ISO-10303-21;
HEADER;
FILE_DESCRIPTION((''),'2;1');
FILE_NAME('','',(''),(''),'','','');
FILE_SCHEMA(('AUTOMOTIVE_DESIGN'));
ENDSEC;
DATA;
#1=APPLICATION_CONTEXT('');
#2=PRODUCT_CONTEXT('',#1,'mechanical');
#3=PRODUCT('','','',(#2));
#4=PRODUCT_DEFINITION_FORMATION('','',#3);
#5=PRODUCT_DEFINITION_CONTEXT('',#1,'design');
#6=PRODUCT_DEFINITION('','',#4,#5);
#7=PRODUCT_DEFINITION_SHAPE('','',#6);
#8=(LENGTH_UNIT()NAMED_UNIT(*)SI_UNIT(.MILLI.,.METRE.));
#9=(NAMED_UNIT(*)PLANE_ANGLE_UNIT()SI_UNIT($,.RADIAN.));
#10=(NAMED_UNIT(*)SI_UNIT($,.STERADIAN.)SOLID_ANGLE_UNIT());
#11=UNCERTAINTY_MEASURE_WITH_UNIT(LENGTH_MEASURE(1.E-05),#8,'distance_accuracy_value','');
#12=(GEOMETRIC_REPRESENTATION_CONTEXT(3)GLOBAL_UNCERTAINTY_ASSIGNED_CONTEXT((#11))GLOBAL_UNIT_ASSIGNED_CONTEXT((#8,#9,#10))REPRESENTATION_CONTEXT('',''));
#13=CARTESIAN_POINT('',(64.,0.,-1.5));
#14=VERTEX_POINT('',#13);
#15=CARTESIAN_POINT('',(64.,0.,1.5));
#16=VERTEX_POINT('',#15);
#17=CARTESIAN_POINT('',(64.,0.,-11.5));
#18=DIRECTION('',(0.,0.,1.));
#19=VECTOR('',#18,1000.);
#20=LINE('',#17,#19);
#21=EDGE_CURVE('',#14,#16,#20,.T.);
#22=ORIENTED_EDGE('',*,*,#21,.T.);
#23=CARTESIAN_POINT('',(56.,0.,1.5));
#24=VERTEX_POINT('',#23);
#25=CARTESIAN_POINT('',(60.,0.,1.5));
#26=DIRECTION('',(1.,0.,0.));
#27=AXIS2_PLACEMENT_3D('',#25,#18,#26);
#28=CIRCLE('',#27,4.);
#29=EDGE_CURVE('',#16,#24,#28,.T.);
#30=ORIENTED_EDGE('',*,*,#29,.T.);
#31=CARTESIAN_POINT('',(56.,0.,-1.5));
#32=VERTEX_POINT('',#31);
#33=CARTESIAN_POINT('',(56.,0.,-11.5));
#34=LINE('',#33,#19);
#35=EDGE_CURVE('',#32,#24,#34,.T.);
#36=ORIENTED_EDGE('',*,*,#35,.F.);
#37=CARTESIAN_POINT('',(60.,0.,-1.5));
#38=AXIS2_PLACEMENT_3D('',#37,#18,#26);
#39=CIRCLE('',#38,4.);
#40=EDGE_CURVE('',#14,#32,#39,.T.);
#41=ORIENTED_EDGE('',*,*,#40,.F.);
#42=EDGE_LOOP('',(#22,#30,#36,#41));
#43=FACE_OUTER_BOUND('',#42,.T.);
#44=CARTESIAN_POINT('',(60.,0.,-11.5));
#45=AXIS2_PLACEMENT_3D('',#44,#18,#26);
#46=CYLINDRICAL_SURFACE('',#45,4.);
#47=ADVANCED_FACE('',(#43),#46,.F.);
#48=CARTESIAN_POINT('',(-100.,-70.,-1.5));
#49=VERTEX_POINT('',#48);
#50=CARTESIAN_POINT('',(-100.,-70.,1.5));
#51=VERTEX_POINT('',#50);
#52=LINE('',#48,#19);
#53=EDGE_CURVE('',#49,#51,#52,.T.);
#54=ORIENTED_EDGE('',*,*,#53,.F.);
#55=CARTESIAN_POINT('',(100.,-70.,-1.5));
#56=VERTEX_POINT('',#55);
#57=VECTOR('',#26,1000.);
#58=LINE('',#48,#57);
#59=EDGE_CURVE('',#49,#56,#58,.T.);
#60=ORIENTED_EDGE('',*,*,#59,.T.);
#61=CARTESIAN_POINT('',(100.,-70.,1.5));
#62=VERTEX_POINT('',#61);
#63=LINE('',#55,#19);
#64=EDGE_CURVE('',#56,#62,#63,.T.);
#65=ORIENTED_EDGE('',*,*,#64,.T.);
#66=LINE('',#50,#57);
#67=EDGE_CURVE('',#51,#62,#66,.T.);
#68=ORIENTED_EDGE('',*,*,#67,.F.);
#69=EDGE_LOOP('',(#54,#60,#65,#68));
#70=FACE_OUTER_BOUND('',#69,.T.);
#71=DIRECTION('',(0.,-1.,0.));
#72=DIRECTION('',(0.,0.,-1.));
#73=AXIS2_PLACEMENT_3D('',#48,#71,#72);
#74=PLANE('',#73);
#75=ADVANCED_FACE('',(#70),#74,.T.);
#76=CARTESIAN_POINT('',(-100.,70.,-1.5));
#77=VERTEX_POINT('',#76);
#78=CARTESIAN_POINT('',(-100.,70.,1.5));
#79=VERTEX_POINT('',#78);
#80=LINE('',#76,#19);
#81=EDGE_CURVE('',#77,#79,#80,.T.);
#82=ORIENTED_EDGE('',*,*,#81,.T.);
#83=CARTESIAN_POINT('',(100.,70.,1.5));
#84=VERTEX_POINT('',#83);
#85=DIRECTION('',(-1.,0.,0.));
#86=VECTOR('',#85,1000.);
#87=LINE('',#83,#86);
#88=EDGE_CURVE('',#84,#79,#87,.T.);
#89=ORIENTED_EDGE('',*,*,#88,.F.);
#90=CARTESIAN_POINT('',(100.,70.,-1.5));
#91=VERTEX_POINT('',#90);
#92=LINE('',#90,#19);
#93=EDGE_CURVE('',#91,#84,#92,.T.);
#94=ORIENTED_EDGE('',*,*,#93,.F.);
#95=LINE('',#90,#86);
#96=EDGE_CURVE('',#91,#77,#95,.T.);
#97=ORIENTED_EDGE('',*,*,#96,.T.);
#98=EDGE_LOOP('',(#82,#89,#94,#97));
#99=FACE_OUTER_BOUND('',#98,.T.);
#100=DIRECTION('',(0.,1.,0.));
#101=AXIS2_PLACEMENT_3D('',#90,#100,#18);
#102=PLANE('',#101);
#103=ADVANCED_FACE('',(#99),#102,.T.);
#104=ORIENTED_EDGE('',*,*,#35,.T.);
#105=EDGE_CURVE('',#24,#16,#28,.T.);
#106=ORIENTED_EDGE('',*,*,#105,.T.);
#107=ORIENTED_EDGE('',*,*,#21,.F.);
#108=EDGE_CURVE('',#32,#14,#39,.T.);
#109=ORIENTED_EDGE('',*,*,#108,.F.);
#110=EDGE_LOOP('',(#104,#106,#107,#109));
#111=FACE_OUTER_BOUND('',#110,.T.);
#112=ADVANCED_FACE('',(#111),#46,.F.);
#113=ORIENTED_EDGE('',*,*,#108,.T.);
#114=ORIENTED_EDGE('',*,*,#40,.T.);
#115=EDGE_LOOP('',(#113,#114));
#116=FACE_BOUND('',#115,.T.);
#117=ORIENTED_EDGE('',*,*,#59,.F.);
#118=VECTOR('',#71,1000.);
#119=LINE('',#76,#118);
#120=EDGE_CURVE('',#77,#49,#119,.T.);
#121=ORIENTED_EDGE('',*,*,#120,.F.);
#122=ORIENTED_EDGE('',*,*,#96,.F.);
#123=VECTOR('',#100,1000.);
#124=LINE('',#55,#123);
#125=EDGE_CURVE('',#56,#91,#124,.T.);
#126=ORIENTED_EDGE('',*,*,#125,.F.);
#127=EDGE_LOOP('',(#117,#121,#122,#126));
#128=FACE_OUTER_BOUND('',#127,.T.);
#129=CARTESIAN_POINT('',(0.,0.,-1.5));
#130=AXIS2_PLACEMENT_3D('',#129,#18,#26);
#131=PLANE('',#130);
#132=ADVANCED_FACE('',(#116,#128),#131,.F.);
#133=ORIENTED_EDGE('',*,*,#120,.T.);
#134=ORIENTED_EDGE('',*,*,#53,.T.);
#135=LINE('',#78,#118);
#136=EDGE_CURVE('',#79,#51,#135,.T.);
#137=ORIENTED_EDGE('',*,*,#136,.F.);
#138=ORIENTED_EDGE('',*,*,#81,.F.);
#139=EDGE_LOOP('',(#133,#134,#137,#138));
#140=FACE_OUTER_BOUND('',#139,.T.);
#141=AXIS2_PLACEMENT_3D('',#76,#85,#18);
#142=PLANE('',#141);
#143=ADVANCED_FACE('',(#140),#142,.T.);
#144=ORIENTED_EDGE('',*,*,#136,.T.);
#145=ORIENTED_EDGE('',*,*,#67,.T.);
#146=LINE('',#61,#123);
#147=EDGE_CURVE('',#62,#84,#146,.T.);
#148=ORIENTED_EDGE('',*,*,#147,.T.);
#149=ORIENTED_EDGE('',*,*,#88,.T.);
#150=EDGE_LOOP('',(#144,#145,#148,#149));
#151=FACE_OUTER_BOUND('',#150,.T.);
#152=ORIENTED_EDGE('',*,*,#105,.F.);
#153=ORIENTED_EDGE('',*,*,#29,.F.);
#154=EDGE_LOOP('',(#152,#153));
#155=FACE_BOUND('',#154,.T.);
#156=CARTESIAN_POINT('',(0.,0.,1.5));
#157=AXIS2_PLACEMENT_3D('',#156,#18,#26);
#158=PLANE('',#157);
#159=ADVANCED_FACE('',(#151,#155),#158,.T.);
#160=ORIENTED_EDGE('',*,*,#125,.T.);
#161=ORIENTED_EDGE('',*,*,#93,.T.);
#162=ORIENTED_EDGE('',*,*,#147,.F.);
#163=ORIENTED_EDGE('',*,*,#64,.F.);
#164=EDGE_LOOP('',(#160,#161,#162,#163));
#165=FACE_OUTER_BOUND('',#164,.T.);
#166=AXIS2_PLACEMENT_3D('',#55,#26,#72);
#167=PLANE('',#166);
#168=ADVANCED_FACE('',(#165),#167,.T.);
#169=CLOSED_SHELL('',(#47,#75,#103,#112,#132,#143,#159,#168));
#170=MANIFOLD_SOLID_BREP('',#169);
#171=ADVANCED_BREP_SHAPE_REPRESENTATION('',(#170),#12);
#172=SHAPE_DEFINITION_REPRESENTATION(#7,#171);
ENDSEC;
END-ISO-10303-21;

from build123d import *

# Parameters (mm, degrees)
SKETCH_1_W          = 200
SKETCH_1_H          = 140
EXTRUDE_1_DEPTH     = 1.5
SKETCH_2_R          = 4
CUT_EXTRUDE_1_DEPTH = 11.5


with BuildPart() as part:
    # 草图1 → 凸台-拉伸1 (new, symmetric)
    with BuildSketch(Plane.XY):
        Rectangle(SKETCH_1_W, SKETCH_1_H)
    extrude(amount=EXTRUDE_1_DEPTH, both=True)

    # 草图2 → 切除-拉伸1 (cut, symmetric)
    with BuildSketch(Plane.XY):
        with Locations((60, 0)):
            Circle(SKETCH_2_R)
    extrude(amount=CUT_EXTRUDE_1_DEPTH, both=True, mode=Mode.SUBTRACT)


solid = part.part
